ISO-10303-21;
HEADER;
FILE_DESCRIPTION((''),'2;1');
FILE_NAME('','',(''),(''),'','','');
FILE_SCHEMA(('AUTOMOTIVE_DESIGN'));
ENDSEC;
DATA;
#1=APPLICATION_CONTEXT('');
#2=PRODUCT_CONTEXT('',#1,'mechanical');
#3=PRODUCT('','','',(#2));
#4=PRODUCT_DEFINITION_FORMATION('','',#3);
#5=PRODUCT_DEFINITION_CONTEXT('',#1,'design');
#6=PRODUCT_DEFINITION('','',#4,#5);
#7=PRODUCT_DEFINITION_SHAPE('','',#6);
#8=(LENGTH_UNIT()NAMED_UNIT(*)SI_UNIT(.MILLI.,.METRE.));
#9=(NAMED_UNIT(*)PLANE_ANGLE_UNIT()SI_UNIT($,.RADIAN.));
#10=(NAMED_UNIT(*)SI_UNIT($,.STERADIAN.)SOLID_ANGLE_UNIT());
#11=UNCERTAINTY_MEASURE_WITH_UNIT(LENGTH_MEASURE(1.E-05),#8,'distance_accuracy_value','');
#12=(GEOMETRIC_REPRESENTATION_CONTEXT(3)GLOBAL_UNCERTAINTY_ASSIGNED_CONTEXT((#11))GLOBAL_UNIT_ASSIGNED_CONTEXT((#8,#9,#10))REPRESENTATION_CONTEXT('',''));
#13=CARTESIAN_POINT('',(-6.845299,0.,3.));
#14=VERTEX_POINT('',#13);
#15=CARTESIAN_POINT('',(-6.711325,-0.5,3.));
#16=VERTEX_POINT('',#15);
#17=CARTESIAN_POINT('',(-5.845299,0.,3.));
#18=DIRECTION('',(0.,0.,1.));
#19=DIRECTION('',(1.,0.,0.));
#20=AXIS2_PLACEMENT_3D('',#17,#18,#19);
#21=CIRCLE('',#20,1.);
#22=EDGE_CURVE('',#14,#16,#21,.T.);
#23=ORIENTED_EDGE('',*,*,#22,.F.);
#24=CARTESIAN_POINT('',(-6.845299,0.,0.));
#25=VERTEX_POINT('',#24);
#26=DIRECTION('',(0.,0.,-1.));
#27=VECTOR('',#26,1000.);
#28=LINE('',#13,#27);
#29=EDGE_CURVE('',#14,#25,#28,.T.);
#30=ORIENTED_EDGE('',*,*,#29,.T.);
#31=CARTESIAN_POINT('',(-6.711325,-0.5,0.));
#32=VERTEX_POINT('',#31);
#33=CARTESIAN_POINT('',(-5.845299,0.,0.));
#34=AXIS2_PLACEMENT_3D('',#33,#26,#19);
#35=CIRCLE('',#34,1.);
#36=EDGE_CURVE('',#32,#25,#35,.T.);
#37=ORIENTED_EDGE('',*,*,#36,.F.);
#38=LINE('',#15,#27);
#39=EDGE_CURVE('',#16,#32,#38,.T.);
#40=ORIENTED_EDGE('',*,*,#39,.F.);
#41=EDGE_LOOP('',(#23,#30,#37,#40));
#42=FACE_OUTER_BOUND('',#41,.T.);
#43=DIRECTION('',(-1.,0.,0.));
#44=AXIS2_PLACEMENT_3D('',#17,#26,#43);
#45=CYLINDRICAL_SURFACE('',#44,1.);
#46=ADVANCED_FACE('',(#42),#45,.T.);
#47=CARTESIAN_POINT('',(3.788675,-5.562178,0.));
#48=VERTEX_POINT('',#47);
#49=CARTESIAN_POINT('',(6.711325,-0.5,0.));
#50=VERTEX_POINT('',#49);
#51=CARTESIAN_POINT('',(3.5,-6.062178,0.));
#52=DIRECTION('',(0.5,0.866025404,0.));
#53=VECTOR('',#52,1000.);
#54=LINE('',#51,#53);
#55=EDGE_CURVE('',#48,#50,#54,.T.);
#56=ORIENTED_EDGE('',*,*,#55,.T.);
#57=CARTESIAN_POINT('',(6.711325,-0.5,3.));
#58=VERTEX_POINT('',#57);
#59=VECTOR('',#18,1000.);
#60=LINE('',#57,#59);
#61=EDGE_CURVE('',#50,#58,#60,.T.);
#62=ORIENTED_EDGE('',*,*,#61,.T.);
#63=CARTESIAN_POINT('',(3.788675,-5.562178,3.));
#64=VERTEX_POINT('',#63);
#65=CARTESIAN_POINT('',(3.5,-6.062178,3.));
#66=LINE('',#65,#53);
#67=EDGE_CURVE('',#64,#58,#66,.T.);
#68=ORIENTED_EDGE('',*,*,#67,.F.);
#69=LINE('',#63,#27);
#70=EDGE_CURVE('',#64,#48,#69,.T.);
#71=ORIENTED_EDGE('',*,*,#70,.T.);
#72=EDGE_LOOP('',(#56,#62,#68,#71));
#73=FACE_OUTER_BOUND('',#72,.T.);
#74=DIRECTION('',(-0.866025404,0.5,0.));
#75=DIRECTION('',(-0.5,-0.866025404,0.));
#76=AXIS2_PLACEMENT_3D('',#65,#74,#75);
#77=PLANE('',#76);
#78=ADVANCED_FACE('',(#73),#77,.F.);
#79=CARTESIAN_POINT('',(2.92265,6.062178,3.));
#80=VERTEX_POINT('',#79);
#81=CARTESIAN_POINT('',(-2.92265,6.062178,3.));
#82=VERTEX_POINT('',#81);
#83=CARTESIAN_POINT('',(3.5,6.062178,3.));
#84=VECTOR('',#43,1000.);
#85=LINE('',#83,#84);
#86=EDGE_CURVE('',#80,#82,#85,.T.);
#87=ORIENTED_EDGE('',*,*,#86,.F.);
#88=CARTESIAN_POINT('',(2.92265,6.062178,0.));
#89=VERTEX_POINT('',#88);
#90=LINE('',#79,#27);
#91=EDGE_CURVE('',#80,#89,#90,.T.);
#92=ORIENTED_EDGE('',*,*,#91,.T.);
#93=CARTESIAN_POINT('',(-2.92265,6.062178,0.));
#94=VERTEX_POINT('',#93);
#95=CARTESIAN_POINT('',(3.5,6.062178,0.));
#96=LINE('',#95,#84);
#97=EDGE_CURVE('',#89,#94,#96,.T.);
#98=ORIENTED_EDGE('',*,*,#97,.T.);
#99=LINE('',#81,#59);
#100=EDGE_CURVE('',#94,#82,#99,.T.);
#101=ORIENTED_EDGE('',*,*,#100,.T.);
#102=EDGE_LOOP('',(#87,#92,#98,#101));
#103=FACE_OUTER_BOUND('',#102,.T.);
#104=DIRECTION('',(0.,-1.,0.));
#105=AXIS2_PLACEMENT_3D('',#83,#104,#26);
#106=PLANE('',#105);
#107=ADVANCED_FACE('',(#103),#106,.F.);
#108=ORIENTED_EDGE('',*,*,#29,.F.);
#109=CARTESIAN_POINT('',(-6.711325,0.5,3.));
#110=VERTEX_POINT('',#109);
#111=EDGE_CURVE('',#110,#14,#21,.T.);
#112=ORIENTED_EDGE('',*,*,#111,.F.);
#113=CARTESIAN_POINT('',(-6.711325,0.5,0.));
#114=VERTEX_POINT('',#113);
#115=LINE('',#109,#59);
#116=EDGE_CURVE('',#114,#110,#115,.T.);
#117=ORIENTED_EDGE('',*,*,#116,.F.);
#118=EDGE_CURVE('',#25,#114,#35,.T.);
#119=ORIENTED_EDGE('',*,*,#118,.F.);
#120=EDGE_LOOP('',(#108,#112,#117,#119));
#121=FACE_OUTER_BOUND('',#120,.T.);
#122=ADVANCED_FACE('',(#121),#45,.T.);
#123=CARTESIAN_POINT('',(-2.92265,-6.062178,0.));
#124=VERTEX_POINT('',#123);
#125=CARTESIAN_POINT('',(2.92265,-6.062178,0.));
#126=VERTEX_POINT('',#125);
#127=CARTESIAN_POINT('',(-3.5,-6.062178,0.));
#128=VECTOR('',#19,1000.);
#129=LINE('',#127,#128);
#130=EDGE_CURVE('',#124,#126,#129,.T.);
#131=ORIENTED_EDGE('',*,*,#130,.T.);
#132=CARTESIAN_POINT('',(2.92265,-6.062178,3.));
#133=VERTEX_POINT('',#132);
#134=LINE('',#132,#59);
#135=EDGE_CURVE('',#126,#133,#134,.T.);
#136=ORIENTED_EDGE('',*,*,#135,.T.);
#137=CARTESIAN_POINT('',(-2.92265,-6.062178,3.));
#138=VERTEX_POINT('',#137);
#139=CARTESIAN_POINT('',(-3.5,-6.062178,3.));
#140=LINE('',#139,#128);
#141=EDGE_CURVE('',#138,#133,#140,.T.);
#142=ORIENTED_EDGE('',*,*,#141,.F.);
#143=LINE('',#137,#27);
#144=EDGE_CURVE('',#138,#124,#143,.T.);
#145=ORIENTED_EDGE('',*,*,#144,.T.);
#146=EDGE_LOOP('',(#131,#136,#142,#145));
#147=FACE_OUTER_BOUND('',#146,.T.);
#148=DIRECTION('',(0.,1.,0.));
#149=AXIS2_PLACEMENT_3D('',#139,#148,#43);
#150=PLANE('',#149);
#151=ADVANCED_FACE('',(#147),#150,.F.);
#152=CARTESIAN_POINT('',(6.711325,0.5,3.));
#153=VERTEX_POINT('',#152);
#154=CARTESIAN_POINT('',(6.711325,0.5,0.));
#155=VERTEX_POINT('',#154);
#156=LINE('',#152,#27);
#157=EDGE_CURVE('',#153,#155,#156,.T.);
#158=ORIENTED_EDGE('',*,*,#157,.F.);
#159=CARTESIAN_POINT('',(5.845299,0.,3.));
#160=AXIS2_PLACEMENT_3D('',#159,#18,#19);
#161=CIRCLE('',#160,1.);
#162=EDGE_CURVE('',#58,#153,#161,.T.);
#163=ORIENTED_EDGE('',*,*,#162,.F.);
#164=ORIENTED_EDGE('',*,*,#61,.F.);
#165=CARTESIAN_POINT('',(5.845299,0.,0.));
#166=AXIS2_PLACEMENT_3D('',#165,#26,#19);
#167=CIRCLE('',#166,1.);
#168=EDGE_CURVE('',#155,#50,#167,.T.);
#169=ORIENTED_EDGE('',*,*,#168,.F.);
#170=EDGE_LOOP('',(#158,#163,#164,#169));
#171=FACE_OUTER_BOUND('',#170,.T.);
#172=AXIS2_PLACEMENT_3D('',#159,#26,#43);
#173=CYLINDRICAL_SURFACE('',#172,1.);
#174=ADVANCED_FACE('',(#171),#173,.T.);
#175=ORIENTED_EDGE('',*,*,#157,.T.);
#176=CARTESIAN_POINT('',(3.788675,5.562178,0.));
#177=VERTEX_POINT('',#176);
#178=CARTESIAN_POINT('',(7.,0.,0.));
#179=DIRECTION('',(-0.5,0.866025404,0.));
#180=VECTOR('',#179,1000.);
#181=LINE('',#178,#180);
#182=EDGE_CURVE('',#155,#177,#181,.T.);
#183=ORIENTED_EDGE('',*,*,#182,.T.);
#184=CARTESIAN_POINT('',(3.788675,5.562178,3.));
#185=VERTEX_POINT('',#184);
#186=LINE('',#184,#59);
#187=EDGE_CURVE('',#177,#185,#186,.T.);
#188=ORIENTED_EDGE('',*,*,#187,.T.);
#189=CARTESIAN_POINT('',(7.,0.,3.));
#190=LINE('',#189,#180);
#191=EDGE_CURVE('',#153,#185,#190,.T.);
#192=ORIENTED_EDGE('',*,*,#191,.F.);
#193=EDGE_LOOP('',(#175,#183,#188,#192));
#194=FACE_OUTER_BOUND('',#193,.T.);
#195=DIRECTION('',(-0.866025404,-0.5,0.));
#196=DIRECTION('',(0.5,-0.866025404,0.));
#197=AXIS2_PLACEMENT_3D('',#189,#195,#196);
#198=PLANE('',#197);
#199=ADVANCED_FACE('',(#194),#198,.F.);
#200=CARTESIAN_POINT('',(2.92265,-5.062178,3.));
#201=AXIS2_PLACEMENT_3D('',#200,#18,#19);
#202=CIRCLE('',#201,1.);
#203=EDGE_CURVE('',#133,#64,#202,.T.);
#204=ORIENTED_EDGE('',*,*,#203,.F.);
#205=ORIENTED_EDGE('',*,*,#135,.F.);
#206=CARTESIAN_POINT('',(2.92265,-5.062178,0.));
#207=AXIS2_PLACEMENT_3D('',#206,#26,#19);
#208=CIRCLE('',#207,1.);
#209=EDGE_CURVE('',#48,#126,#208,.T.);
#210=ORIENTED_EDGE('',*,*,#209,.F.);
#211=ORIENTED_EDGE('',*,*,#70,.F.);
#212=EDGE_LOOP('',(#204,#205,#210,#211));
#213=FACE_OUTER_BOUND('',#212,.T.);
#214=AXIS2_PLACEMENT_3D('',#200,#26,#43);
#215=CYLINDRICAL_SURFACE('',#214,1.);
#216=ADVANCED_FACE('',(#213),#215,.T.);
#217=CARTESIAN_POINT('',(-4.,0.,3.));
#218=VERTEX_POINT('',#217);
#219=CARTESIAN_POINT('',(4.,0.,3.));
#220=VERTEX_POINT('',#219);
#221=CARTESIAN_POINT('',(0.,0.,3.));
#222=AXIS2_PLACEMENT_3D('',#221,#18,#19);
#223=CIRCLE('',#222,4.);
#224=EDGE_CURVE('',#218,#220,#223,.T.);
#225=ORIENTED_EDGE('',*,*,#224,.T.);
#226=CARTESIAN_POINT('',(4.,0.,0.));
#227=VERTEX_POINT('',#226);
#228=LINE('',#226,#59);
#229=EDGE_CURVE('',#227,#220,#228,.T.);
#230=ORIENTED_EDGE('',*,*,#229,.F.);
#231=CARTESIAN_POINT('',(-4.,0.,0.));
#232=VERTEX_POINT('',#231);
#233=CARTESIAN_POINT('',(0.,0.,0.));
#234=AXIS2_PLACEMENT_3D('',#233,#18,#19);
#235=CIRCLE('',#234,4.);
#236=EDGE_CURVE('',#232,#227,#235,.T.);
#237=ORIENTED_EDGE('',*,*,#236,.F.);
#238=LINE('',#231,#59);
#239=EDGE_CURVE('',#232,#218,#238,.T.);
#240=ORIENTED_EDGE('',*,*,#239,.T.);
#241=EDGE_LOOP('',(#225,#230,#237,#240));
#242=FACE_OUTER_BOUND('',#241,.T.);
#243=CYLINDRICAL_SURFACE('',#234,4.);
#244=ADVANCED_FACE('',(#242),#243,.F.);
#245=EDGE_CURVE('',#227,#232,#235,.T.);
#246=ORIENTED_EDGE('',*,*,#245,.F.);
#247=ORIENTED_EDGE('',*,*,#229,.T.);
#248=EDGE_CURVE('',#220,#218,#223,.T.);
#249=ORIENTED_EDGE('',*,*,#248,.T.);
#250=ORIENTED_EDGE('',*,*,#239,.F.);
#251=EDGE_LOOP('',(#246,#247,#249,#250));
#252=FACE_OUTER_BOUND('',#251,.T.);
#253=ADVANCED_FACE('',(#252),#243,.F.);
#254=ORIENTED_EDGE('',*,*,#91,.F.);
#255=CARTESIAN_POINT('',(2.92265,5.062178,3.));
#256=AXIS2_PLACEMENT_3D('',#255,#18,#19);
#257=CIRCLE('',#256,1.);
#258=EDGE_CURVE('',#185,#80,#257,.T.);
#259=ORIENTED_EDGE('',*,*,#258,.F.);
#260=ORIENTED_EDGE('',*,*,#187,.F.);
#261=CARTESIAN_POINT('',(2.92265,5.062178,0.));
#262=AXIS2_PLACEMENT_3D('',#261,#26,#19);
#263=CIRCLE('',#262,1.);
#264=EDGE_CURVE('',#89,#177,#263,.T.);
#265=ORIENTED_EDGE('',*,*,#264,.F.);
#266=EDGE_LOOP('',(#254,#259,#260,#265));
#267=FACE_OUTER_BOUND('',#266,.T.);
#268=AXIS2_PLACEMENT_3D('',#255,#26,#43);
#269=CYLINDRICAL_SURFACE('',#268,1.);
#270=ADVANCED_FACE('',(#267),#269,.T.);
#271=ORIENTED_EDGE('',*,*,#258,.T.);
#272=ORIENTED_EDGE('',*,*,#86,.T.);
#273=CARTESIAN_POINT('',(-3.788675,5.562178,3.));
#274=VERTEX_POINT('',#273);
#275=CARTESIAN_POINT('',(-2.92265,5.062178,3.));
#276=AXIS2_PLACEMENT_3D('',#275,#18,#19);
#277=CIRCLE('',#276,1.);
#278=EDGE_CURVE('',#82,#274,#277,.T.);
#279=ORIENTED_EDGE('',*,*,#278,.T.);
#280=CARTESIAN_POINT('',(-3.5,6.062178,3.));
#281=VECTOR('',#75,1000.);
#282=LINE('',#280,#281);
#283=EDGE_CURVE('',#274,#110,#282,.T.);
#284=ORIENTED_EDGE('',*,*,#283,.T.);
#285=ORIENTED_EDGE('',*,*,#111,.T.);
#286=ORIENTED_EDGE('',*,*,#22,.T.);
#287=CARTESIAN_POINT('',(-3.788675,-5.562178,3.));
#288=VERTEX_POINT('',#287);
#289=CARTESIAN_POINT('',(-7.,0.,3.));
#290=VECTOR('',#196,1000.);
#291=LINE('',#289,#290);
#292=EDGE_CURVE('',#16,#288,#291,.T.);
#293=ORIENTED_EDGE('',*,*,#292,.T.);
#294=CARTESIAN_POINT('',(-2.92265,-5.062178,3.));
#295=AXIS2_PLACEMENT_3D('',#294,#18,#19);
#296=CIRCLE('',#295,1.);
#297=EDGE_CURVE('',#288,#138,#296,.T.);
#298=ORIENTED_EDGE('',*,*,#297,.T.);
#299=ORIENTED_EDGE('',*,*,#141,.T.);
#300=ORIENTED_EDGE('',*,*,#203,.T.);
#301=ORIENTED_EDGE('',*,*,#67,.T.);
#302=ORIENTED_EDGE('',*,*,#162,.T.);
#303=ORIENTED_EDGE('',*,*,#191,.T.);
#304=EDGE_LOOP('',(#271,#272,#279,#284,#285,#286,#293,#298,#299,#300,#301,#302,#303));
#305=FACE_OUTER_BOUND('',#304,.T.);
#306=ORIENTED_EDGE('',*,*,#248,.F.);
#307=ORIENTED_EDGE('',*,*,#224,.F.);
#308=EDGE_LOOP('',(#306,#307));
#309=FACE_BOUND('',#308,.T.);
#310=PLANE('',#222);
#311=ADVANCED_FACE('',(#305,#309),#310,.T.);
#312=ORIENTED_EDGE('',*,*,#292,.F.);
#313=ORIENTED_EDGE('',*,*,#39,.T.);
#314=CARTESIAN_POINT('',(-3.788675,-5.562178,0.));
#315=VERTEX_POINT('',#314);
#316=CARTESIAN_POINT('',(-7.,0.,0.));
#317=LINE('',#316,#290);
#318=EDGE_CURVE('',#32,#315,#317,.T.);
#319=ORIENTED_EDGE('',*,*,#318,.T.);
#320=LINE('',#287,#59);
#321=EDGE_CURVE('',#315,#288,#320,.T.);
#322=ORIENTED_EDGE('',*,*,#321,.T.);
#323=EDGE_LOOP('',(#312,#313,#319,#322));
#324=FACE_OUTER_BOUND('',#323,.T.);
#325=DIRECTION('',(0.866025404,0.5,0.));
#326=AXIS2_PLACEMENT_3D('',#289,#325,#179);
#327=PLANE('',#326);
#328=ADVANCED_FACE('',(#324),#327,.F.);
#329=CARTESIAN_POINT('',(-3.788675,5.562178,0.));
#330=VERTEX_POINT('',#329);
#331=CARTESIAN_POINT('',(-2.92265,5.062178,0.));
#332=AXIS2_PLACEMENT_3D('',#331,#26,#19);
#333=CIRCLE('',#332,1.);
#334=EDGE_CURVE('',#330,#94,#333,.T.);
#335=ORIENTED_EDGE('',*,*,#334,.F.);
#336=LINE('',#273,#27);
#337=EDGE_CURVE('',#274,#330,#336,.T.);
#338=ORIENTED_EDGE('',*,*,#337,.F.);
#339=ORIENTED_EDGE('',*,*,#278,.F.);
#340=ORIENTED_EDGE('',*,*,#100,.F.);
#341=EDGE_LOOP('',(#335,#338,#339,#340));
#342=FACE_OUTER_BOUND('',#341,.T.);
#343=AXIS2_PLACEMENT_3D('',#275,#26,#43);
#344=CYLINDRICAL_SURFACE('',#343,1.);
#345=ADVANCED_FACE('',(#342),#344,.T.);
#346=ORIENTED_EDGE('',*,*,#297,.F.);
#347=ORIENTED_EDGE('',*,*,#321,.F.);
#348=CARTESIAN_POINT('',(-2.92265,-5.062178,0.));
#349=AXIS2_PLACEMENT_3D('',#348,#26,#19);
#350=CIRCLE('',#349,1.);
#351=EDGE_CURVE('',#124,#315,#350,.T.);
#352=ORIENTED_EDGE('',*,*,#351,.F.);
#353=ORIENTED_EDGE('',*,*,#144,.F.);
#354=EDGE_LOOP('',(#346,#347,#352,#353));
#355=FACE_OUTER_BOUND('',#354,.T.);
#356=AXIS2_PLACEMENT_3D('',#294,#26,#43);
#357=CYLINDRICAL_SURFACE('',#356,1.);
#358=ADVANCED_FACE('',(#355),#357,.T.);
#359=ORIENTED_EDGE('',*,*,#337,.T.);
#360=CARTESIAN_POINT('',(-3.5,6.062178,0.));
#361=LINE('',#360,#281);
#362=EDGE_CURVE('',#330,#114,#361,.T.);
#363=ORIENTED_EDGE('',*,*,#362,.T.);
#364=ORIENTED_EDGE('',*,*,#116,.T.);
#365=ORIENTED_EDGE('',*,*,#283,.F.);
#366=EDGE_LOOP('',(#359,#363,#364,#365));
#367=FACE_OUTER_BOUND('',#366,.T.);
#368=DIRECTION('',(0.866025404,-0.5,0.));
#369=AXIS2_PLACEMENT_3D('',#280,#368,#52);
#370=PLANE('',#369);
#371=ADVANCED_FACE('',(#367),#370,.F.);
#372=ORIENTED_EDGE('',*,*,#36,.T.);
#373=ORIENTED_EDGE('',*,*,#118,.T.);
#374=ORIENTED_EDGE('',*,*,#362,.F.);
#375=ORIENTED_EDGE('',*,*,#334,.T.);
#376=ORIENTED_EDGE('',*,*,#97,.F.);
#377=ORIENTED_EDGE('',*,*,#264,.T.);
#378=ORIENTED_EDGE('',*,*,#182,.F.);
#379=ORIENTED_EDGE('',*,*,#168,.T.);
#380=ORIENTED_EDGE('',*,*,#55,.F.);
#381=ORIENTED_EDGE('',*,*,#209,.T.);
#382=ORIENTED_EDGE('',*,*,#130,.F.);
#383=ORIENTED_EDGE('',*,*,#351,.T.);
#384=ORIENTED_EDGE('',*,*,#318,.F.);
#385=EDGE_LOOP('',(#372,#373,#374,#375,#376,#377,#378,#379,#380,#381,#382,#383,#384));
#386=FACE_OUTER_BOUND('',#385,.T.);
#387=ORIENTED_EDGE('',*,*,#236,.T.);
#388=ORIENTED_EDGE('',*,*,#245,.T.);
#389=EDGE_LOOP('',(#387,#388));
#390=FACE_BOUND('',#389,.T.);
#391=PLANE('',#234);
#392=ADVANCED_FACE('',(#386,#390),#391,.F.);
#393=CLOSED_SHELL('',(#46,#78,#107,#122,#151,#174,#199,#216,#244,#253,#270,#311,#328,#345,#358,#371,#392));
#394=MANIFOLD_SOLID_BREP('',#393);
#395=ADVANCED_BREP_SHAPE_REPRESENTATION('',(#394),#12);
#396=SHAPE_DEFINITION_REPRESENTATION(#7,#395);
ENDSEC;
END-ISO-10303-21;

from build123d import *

# Parameters (mm, degrees)
HEX_BODY_DEPTH          = 3
HEX_CORNER_FILLETS_R1_R = 1
BORE_SKETCH_R           = 4
BORE_8_DEPTH            = 3


with BuildPart() as part:
    # Hex Profile Sketch → Hex Body (new body)
    with BuildSketch(Plane.XY):
        Polygon((3.5, -6.062177826), (7, 0), (3.5, 6.062177826), (-3.5, 6.062177826), (-7, 0), (-3.5, -6.062177826), align=None)
    extrude(amount=HEX_BODY_DEPTH)

    # Hex Corner Fillets R1
    hex_corner_fillets_r1_edges = [part.edges().sort_by_distance(p)[0] for p in [
        (-3.5, -6.062177826, 1.5),
        (-7, 0, 1.5),
        (-3.5, 6.062177826, 1.5),
        (3.5, 6.062177826, 1.5),
        (7, 0, 1.5),
        (3.5, -6.062177826, 1.5),
    ]]
    fillet(hex_corner_fillets_r1_edges, radius=HEX_CORNER_FILLETS_R1_R)

    # Bore Sketch → Bore Ø8 (cut)
    with BuildSketch(Plane.XY.offset(3)):
        Circle(BORE_SKETCH_R)
    extrude(amount=-BORE_8_DEPTH, mode=Mode.SUBTRACT)


solid = part.part
